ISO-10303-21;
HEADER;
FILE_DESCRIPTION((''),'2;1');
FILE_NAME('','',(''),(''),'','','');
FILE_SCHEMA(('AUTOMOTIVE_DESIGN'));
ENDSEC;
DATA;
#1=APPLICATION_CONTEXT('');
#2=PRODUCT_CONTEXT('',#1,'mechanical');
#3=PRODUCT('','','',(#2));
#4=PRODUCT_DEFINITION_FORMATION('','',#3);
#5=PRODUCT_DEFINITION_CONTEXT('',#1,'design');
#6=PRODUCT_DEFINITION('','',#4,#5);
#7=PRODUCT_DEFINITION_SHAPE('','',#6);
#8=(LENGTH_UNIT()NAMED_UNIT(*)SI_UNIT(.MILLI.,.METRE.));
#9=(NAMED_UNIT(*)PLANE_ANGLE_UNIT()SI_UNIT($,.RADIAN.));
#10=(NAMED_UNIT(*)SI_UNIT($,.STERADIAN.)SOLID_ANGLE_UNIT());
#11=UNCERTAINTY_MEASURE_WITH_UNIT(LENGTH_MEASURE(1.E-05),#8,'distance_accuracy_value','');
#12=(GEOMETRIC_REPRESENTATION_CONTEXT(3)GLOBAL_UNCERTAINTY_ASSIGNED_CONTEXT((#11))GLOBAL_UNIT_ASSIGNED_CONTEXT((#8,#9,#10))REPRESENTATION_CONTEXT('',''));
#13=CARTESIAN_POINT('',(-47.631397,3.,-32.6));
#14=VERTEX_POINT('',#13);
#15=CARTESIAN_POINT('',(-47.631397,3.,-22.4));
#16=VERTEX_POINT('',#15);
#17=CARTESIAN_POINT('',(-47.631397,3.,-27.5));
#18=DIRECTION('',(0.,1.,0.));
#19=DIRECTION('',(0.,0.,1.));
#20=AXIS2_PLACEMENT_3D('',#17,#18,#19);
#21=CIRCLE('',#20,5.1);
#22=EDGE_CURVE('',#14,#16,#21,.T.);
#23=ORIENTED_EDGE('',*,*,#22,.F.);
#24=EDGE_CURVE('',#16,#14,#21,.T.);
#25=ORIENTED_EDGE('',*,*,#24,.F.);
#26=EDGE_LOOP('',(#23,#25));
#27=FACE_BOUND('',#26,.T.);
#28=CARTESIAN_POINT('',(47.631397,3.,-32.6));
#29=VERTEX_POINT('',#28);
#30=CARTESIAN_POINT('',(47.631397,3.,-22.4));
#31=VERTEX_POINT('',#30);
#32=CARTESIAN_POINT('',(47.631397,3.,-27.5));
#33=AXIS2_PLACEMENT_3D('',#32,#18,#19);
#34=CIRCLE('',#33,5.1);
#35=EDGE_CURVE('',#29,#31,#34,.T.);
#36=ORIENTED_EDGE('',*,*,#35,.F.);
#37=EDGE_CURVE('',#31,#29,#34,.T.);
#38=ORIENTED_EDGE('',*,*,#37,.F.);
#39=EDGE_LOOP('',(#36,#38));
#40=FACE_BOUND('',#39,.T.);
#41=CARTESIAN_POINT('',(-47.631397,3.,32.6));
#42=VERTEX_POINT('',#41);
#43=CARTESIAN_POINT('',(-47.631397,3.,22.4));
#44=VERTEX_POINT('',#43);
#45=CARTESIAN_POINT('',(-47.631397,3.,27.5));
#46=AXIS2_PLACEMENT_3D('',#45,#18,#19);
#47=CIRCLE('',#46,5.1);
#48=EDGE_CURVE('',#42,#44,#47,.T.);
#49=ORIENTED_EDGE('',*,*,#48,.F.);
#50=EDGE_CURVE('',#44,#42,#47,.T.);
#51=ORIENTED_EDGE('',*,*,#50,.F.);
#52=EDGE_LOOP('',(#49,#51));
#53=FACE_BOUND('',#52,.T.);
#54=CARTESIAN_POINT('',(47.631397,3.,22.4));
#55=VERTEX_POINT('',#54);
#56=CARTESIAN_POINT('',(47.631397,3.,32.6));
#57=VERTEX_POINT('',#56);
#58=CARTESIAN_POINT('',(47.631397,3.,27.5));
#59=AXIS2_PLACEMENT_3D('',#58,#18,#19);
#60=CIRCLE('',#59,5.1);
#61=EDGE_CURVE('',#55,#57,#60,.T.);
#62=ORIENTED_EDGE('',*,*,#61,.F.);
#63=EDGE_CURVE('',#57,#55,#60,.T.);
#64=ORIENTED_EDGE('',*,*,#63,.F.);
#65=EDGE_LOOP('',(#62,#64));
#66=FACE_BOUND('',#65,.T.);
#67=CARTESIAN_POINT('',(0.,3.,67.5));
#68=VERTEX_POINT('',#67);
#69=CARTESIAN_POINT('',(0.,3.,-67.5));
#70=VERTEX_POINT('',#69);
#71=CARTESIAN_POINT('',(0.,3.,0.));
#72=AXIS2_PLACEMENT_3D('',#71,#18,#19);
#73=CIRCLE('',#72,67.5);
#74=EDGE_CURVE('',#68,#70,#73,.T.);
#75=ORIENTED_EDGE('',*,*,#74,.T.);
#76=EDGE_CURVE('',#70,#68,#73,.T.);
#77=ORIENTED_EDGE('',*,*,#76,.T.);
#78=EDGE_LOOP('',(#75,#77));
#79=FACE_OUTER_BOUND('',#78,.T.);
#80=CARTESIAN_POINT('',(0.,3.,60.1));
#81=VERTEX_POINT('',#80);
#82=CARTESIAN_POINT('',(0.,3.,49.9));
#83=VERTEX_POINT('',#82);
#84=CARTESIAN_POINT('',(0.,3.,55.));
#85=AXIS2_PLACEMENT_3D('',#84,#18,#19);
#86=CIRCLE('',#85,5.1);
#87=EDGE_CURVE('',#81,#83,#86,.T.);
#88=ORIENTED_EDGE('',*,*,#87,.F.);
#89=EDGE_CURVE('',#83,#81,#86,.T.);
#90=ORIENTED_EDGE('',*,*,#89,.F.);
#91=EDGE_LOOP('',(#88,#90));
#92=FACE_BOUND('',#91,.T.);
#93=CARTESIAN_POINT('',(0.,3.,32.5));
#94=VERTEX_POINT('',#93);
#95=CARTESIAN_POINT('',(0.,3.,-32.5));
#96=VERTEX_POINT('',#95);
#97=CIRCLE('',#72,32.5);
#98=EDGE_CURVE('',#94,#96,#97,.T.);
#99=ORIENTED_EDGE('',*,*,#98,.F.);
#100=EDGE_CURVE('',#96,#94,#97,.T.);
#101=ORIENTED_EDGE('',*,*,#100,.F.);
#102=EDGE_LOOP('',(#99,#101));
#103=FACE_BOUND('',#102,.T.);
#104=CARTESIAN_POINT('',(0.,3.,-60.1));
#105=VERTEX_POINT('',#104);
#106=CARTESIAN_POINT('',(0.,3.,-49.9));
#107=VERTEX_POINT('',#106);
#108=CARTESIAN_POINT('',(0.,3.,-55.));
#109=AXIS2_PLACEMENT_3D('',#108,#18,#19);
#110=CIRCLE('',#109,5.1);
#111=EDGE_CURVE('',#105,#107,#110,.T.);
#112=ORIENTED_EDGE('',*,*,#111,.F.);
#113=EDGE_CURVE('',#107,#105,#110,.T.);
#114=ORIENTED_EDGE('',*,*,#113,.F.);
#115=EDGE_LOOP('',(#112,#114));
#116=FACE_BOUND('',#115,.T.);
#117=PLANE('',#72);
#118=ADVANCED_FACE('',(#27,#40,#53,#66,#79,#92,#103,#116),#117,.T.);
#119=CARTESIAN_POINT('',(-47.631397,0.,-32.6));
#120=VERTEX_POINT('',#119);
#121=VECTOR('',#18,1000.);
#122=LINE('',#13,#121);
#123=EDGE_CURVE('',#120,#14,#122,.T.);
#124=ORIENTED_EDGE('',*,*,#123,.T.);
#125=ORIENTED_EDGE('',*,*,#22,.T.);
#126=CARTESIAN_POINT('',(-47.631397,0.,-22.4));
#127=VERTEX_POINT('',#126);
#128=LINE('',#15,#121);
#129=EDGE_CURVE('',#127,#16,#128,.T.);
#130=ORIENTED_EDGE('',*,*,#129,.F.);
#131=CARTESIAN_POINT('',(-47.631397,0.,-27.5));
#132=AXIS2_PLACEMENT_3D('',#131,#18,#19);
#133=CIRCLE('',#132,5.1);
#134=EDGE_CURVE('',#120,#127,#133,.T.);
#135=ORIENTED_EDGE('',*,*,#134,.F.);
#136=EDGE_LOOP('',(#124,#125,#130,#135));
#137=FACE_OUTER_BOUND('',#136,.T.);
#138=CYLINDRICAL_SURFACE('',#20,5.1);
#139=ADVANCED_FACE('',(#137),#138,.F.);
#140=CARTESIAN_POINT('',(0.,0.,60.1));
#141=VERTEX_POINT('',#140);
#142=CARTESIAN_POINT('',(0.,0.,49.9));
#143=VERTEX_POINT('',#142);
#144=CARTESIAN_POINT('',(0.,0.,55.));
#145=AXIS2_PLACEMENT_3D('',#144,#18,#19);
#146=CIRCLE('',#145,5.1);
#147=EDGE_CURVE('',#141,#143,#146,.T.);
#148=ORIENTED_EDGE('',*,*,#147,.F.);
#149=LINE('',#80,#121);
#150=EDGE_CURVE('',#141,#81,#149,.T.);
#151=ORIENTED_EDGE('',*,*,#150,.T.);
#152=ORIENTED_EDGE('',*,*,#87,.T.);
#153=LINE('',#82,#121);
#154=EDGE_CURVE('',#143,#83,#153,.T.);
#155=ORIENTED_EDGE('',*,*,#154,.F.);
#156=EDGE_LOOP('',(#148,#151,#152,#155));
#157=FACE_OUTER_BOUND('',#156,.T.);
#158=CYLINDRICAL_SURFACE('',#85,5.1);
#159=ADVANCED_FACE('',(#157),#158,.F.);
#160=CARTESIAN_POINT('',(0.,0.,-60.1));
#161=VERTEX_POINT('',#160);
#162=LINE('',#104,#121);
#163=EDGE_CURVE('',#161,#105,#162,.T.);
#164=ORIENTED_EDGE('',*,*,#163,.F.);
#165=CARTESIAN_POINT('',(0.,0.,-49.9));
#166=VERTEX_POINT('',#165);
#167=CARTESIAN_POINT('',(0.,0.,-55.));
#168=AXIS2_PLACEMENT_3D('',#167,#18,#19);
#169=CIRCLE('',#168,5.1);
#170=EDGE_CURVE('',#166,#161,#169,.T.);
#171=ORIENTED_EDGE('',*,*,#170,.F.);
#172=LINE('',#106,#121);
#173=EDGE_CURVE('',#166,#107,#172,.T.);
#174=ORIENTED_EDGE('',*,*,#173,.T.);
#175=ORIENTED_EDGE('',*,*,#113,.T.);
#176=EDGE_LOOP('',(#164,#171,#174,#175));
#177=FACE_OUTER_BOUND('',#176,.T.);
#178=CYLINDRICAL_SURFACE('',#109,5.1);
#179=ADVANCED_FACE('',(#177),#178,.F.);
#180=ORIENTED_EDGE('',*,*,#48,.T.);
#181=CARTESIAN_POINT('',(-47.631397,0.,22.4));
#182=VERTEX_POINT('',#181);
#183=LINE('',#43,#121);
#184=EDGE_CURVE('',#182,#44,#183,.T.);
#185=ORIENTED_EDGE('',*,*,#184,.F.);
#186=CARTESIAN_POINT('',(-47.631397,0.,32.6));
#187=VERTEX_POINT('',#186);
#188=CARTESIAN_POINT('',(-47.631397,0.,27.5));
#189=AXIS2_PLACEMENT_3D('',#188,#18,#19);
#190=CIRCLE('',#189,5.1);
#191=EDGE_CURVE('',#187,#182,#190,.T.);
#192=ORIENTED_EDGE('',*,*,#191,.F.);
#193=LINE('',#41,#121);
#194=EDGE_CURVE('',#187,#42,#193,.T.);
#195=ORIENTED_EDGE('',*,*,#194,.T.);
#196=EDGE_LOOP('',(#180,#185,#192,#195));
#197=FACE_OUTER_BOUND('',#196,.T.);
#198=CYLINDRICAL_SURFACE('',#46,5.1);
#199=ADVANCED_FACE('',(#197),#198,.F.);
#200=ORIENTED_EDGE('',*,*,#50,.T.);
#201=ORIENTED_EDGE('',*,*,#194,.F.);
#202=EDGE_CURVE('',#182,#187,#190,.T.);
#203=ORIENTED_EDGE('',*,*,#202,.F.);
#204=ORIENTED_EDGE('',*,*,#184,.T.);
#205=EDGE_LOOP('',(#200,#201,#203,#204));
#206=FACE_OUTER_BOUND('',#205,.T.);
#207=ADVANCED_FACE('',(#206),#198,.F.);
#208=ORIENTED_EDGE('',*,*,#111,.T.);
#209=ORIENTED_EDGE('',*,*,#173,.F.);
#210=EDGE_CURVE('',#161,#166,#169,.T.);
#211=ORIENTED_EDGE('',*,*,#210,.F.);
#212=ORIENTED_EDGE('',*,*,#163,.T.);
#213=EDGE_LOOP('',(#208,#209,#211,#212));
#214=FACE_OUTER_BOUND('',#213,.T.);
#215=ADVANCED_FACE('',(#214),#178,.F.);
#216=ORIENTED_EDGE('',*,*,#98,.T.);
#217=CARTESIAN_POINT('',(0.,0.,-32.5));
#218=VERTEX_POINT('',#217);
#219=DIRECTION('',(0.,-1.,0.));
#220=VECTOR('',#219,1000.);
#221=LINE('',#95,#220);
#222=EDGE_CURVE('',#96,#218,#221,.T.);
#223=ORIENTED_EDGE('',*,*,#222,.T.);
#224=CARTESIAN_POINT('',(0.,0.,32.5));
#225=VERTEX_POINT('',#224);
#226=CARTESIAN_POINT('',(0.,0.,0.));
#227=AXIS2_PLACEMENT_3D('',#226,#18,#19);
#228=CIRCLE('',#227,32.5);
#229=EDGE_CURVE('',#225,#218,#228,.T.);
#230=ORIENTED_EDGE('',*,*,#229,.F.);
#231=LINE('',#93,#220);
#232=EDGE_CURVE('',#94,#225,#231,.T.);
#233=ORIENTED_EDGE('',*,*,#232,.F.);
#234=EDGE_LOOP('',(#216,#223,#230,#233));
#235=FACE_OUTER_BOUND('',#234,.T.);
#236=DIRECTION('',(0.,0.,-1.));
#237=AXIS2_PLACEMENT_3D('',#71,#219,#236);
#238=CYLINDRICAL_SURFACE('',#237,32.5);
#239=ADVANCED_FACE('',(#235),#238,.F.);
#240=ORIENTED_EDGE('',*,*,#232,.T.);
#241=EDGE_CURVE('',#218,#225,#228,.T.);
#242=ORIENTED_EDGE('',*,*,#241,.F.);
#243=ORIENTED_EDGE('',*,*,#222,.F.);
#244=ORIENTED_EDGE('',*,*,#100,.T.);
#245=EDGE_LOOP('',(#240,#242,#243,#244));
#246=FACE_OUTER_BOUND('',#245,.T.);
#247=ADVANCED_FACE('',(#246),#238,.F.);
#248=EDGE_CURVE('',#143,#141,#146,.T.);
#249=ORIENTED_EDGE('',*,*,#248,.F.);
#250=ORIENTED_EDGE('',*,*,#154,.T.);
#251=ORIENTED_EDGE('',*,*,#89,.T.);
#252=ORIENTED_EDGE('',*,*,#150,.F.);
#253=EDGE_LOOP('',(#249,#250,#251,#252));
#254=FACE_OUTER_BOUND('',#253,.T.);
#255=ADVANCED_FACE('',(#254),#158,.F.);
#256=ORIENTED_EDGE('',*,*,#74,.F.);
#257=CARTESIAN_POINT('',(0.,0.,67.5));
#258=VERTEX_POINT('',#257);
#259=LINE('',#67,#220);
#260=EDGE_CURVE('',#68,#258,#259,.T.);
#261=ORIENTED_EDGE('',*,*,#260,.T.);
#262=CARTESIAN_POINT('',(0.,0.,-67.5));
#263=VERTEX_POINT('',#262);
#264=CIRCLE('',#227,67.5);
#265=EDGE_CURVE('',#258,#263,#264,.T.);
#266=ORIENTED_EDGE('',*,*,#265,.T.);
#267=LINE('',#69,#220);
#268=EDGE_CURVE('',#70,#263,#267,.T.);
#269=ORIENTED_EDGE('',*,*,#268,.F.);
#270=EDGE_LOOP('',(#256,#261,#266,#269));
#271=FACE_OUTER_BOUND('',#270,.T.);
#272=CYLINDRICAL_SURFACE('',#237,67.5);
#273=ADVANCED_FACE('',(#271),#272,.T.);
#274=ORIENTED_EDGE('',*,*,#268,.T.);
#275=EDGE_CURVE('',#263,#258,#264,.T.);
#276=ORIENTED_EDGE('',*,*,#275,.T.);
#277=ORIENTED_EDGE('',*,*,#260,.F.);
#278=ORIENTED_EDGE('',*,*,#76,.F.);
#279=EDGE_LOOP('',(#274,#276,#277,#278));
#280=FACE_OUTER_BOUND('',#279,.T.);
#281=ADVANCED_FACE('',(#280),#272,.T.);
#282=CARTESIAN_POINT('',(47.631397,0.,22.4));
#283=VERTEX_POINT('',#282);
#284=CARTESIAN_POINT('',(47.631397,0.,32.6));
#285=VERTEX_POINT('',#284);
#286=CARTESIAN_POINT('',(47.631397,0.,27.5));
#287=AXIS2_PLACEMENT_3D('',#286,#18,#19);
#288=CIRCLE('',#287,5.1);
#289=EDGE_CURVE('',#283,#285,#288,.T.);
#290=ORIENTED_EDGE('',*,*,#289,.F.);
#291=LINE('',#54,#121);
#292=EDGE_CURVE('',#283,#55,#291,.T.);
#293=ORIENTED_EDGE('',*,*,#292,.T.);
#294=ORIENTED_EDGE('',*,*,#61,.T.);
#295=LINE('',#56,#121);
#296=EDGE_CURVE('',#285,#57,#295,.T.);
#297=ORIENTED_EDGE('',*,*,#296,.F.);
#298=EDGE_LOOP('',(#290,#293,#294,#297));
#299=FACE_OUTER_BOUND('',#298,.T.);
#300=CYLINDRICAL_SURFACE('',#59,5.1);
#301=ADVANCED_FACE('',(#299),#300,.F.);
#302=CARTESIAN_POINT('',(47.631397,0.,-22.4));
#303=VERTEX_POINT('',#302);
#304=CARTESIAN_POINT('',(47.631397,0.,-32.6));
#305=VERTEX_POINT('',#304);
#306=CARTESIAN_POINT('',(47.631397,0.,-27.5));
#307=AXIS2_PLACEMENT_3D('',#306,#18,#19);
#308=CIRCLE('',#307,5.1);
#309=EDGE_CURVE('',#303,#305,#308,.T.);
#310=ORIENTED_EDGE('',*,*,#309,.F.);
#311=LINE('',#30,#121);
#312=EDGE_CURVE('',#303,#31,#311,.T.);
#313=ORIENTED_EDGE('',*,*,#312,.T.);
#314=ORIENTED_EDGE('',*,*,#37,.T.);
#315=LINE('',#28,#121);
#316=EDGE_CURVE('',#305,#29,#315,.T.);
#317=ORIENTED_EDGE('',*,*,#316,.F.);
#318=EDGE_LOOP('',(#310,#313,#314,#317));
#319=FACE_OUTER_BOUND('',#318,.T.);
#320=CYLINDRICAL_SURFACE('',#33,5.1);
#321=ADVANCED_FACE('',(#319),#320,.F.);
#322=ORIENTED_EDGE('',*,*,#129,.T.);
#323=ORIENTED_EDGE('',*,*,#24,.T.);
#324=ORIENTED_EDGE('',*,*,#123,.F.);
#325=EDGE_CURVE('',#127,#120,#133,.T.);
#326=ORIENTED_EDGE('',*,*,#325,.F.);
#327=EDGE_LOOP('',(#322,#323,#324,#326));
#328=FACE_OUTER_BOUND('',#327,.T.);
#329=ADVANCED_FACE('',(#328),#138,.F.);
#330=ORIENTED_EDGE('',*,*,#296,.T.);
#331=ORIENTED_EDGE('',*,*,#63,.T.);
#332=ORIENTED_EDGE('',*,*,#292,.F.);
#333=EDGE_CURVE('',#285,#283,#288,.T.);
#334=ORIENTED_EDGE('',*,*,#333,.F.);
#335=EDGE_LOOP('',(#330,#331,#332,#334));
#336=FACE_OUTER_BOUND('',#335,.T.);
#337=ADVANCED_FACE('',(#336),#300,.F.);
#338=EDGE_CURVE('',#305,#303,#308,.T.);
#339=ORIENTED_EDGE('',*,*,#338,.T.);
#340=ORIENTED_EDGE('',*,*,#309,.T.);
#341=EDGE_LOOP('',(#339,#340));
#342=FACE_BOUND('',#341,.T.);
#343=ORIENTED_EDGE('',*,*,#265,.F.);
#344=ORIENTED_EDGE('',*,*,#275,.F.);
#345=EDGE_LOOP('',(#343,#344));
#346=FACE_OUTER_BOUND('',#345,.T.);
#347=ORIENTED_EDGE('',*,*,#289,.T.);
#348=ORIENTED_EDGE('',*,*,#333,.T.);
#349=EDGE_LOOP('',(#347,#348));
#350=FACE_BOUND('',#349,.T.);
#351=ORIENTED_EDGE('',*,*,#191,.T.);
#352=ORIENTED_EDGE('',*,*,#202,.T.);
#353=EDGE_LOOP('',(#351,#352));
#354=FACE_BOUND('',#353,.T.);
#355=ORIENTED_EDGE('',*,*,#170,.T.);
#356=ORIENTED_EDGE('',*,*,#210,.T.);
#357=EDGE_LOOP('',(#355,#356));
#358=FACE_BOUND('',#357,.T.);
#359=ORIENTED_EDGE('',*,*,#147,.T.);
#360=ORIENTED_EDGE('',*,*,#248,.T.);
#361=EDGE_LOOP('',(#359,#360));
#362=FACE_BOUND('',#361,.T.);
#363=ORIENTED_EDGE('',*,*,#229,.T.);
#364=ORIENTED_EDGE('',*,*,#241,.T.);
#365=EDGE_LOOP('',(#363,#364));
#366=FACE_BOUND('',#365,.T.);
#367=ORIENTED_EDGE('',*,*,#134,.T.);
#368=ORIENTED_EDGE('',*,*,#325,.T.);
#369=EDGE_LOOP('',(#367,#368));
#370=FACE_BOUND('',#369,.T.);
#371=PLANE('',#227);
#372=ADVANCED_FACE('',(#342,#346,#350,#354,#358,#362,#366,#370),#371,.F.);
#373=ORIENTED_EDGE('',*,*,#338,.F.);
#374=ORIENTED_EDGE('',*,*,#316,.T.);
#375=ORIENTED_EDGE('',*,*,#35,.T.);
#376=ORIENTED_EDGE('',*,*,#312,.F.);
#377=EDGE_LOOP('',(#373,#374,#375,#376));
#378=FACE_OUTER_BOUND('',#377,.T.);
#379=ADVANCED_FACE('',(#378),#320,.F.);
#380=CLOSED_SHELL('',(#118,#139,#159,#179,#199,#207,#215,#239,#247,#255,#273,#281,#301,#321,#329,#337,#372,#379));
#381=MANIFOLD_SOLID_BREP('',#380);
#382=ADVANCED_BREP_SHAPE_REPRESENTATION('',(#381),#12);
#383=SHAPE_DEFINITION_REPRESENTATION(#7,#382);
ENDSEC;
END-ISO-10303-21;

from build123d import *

# Parameters (mm, degrees)
SKETCH_1_R              = 67.5
SKETCH_1_R_2            = 32.5
EXTRUDE_1_DEPTH         = 3
HOLE_WIZARD_M12_1_D     = 10.2
HOLE_WIZARD_M12_1_DEPTH = 5
HOLE_WIZARD_M12_1_TIP   = 3.064389157


with BuildPart() as part:
    # 草图1 → 凸台-拉伸1 (new body)
    with BuildSketch(Plane(origin=(0, 0, 0), x_dir=(1, 0, 0), z_dir=(0, 1, 0))):
        with Locations(Location((0, 0, 0), (0, 0, 270))):
            Circle(SKETCH_1_R)
        with Locations(Location((0, 0, 0), (0, 0, 270))):
            Circle(SKETCH_1_R_2, mode=Mode.SUBTRACT)
    extrude(amount=EXTRUDE_1_DEPTH)

    # M12 螺纹孔的螺纹孔钻头1
    with Locations(Plane(origin=(0, 3, 0), x_dir=(1, 0, 0), z_dir=(0, 1, 0))):
        with Locations((0, 55), (-47.631397208, 27.5), (-47.631397208, -27.5), (0, -55), (47.631397208, -27.5), (47.631397208, 27.5)):
            Hole(HOLE_WIZARD_M12_1_D / 2, depth=HOLE_WIZARD_M12_1_DEPTH)
            with Locations((0, 0, -(HOLE_WIZARD_M12_1_DEPTH + HOLE_WIZARD_M12_1_TIP / 2))):  # 118° drill point
                Cone(0, HOLE_WIZARD_M12_1_D / 2, HOLE_WIZARD_M12_1_TIP, mode=Mode.SUBTRACT)


solid = part.part
